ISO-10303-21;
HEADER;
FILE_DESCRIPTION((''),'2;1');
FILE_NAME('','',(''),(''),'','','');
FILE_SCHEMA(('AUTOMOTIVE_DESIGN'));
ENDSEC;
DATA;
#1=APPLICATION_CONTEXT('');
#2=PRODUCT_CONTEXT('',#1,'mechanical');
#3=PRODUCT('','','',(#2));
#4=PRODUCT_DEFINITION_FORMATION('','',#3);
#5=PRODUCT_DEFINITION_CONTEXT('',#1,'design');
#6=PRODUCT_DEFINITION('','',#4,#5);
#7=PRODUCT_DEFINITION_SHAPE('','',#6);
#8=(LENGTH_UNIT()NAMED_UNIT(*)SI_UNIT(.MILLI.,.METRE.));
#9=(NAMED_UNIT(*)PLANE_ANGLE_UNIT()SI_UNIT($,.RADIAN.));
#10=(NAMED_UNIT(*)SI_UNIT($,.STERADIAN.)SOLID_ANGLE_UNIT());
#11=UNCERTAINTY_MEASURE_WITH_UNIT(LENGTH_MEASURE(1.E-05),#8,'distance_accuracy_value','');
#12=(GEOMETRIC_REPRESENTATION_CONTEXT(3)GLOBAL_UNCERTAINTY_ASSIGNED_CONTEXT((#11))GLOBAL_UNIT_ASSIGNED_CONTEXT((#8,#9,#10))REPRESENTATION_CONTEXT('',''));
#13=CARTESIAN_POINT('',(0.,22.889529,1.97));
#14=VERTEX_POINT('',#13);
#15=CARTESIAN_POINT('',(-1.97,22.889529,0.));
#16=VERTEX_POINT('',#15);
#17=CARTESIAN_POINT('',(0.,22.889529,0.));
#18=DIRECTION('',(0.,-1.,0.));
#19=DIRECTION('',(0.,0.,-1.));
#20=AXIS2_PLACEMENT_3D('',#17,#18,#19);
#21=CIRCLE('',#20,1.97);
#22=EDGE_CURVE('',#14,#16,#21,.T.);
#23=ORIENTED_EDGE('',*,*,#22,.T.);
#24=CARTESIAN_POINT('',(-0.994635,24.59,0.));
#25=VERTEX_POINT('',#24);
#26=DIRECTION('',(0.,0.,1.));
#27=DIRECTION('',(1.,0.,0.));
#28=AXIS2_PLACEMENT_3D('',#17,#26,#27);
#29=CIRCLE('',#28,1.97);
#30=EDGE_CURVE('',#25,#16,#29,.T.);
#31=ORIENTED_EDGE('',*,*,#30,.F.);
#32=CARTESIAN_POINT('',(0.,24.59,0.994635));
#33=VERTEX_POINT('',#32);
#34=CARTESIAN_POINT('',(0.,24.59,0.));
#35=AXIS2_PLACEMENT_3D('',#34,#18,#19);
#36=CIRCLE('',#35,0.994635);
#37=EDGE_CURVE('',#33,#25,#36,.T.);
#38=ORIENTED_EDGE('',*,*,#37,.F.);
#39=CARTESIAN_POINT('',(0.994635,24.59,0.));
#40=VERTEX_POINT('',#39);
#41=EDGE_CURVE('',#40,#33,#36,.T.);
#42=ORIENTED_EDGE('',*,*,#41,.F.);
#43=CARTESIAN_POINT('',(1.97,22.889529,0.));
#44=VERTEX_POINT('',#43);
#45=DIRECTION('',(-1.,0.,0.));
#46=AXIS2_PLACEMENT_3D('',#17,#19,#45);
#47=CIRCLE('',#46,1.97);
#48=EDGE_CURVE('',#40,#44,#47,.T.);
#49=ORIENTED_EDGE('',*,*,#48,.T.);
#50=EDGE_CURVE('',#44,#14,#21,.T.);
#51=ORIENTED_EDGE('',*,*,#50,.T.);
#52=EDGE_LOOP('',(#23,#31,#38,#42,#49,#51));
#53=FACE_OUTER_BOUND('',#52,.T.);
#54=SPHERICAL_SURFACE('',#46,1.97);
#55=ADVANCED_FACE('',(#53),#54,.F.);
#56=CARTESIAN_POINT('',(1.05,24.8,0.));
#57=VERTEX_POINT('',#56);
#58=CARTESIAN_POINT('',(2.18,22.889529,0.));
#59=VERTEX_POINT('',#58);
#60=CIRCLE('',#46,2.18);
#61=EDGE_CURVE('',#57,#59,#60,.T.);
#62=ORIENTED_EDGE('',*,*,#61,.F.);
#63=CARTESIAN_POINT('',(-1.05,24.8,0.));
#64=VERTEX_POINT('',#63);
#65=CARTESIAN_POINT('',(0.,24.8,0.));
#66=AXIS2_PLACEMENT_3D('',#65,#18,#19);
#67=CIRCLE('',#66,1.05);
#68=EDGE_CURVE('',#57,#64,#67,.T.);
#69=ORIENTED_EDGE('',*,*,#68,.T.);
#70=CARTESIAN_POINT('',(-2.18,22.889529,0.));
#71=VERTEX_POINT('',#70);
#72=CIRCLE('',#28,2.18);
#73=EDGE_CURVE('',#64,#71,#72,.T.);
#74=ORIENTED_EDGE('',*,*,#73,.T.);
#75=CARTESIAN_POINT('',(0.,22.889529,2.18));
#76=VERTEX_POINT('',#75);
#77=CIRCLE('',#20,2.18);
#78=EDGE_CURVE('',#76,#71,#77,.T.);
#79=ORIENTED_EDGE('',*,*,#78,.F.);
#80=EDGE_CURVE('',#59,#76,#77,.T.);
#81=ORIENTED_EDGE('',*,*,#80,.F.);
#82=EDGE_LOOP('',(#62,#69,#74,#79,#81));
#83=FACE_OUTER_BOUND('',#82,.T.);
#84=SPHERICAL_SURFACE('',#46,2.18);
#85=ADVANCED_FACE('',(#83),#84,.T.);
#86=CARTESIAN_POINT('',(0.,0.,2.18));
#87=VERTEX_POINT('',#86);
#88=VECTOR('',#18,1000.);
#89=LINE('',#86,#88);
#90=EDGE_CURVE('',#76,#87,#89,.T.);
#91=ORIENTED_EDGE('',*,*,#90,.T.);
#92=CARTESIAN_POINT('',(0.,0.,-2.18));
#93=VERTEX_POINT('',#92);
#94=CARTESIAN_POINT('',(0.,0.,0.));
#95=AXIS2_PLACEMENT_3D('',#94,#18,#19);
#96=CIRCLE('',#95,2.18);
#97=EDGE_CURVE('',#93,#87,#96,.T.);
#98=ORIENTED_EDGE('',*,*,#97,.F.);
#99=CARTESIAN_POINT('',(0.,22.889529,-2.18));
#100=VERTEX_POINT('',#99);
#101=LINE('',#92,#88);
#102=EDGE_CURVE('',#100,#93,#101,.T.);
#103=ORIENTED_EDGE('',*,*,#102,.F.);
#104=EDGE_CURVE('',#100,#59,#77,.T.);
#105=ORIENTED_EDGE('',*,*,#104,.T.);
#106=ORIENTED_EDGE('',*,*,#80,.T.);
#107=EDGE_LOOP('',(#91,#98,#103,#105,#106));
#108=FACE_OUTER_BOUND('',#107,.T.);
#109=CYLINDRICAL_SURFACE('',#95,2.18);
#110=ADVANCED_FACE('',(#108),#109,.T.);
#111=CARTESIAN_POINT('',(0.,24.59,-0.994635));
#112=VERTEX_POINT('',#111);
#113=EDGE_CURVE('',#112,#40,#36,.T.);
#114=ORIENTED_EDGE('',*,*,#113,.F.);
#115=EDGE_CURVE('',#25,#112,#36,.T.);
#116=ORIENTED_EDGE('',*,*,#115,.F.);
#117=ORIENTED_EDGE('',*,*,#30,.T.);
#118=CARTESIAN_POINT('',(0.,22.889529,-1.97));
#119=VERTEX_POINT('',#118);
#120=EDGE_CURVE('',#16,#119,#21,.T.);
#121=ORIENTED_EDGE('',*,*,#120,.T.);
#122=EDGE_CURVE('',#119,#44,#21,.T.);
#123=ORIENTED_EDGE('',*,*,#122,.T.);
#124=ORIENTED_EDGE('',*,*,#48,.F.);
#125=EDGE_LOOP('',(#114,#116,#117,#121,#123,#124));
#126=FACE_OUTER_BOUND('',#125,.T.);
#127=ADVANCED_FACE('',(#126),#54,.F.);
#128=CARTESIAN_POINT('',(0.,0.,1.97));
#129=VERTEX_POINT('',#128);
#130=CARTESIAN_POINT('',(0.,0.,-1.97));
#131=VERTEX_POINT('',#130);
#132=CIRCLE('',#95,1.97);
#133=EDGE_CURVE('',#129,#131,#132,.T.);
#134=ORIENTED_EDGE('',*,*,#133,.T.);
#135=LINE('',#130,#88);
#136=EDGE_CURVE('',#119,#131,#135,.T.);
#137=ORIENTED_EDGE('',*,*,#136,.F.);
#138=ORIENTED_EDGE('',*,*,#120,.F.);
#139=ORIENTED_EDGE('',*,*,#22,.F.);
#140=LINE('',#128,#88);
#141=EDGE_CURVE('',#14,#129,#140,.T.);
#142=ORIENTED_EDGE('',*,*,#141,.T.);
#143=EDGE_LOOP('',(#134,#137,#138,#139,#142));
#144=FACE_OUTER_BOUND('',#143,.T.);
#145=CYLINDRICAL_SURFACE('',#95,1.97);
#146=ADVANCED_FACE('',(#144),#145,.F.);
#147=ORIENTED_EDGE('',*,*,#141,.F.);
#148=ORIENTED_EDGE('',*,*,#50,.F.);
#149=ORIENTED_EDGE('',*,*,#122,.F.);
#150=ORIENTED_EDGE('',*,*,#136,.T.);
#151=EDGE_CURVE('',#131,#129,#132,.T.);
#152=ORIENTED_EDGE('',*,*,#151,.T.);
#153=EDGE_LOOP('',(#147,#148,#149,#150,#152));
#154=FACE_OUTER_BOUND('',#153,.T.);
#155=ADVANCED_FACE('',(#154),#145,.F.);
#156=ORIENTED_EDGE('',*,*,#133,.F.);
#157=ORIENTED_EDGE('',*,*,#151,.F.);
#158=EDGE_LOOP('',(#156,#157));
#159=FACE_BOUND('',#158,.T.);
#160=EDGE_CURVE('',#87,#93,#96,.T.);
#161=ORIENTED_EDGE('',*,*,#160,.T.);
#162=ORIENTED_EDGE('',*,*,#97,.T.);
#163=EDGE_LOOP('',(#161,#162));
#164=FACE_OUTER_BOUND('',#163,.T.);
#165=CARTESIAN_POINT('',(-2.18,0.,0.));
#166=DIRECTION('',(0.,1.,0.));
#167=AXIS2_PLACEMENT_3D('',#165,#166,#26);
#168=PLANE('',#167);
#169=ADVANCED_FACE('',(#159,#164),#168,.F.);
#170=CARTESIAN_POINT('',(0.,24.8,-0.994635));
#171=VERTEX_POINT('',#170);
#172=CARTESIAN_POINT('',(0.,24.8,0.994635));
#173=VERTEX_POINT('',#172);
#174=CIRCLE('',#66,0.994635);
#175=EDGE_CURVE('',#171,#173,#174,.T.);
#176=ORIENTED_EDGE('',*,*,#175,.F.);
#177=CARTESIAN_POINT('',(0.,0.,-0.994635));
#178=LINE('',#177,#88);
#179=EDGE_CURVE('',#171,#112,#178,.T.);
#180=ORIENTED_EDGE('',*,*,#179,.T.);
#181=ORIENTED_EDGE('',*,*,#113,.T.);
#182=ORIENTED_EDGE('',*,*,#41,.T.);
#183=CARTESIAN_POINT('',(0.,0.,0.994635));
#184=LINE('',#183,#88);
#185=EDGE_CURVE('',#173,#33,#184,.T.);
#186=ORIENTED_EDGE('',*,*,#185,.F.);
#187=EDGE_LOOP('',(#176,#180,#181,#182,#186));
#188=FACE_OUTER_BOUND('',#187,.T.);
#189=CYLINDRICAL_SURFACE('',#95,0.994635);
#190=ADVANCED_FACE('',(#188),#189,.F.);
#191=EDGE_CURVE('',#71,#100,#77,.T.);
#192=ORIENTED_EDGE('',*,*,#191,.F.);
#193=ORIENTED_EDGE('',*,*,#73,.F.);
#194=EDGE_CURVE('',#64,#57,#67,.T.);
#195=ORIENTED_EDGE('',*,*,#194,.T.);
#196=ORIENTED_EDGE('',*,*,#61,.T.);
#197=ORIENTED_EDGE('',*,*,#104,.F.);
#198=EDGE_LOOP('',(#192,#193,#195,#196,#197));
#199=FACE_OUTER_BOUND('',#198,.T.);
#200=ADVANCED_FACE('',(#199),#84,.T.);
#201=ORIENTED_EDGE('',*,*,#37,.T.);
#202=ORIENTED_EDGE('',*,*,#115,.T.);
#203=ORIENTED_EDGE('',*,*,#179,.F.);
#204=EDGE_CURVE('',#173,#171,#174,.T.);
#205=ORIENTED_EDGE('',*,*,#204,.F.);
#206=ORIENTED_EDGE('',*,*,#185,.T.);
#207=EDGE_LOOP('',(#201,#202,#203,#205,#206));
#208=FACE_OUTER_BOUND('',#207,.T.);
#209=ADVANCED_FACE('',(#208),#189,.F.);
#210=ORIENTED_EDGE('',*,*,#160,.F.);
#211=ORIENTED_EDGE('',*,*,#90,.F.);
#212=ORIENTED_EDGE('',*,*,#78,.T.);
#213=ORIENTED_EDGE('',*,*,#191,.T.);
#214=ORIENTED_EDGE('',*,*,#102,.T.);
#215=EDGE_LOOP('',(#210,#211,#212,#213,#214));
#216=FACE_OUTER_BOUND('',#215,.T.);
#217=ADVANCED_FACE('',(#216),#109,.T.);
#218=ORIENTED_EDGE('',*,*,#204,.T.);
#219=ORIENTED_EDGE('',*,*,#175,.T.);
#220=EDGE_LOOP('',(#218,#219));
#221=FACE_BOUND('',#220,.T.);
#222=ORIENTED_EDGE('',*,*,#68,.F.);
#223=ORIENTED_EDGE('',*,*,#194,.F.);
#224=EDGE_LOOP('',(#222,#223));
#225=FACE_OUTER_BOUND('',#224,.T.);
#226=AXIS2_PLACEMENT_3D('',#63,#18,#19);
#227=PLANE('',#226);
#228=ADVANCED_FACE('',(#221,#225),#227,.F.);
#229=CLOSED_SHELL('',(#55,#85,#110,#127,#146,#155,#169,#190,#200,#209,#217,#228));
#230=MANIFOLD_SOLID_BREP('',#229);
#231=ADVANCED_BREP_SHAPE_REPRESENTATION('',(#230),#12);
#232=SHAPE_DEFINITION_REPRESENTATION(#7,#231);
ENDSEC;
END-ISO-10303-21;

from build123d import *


with BuildPart() as part:
    # Sketch1 → Revolve1 (revolve)
    with BuildSketch(Plane.XY, mode=Mode.PRIVATE) as revolve1_sk:
        with BuildLine():
            Line((-2.18, 0), (-2.18, 22.889528854))
            ThreePointArc((-2.18, 22.889528854), (-1.876352845, 23.999348659), (-1.05, 24.8))
            Line((-1.05, 24.8), (-0.994634547, 24.8))
            Line((-0.994634547, 24.8), (-0.994634547, 24.59))
            ThreePointArc((-0.994634547, 24.59), (-1.708849036, 23.869699743), (-1.97, 22.889528854))
            Line((-1.97, 22.889528854), (-1.97, 0))
            Line((-1.97, 0), (-2.18, 0))
        make_face()
    revolve(revolve1_sk.sketch.rotate(Axis((0, 0, 0), (0, 1, 0)), 270), axis=Axis((0, 0, 0), (0, 1, 0)))


solid = part.part
